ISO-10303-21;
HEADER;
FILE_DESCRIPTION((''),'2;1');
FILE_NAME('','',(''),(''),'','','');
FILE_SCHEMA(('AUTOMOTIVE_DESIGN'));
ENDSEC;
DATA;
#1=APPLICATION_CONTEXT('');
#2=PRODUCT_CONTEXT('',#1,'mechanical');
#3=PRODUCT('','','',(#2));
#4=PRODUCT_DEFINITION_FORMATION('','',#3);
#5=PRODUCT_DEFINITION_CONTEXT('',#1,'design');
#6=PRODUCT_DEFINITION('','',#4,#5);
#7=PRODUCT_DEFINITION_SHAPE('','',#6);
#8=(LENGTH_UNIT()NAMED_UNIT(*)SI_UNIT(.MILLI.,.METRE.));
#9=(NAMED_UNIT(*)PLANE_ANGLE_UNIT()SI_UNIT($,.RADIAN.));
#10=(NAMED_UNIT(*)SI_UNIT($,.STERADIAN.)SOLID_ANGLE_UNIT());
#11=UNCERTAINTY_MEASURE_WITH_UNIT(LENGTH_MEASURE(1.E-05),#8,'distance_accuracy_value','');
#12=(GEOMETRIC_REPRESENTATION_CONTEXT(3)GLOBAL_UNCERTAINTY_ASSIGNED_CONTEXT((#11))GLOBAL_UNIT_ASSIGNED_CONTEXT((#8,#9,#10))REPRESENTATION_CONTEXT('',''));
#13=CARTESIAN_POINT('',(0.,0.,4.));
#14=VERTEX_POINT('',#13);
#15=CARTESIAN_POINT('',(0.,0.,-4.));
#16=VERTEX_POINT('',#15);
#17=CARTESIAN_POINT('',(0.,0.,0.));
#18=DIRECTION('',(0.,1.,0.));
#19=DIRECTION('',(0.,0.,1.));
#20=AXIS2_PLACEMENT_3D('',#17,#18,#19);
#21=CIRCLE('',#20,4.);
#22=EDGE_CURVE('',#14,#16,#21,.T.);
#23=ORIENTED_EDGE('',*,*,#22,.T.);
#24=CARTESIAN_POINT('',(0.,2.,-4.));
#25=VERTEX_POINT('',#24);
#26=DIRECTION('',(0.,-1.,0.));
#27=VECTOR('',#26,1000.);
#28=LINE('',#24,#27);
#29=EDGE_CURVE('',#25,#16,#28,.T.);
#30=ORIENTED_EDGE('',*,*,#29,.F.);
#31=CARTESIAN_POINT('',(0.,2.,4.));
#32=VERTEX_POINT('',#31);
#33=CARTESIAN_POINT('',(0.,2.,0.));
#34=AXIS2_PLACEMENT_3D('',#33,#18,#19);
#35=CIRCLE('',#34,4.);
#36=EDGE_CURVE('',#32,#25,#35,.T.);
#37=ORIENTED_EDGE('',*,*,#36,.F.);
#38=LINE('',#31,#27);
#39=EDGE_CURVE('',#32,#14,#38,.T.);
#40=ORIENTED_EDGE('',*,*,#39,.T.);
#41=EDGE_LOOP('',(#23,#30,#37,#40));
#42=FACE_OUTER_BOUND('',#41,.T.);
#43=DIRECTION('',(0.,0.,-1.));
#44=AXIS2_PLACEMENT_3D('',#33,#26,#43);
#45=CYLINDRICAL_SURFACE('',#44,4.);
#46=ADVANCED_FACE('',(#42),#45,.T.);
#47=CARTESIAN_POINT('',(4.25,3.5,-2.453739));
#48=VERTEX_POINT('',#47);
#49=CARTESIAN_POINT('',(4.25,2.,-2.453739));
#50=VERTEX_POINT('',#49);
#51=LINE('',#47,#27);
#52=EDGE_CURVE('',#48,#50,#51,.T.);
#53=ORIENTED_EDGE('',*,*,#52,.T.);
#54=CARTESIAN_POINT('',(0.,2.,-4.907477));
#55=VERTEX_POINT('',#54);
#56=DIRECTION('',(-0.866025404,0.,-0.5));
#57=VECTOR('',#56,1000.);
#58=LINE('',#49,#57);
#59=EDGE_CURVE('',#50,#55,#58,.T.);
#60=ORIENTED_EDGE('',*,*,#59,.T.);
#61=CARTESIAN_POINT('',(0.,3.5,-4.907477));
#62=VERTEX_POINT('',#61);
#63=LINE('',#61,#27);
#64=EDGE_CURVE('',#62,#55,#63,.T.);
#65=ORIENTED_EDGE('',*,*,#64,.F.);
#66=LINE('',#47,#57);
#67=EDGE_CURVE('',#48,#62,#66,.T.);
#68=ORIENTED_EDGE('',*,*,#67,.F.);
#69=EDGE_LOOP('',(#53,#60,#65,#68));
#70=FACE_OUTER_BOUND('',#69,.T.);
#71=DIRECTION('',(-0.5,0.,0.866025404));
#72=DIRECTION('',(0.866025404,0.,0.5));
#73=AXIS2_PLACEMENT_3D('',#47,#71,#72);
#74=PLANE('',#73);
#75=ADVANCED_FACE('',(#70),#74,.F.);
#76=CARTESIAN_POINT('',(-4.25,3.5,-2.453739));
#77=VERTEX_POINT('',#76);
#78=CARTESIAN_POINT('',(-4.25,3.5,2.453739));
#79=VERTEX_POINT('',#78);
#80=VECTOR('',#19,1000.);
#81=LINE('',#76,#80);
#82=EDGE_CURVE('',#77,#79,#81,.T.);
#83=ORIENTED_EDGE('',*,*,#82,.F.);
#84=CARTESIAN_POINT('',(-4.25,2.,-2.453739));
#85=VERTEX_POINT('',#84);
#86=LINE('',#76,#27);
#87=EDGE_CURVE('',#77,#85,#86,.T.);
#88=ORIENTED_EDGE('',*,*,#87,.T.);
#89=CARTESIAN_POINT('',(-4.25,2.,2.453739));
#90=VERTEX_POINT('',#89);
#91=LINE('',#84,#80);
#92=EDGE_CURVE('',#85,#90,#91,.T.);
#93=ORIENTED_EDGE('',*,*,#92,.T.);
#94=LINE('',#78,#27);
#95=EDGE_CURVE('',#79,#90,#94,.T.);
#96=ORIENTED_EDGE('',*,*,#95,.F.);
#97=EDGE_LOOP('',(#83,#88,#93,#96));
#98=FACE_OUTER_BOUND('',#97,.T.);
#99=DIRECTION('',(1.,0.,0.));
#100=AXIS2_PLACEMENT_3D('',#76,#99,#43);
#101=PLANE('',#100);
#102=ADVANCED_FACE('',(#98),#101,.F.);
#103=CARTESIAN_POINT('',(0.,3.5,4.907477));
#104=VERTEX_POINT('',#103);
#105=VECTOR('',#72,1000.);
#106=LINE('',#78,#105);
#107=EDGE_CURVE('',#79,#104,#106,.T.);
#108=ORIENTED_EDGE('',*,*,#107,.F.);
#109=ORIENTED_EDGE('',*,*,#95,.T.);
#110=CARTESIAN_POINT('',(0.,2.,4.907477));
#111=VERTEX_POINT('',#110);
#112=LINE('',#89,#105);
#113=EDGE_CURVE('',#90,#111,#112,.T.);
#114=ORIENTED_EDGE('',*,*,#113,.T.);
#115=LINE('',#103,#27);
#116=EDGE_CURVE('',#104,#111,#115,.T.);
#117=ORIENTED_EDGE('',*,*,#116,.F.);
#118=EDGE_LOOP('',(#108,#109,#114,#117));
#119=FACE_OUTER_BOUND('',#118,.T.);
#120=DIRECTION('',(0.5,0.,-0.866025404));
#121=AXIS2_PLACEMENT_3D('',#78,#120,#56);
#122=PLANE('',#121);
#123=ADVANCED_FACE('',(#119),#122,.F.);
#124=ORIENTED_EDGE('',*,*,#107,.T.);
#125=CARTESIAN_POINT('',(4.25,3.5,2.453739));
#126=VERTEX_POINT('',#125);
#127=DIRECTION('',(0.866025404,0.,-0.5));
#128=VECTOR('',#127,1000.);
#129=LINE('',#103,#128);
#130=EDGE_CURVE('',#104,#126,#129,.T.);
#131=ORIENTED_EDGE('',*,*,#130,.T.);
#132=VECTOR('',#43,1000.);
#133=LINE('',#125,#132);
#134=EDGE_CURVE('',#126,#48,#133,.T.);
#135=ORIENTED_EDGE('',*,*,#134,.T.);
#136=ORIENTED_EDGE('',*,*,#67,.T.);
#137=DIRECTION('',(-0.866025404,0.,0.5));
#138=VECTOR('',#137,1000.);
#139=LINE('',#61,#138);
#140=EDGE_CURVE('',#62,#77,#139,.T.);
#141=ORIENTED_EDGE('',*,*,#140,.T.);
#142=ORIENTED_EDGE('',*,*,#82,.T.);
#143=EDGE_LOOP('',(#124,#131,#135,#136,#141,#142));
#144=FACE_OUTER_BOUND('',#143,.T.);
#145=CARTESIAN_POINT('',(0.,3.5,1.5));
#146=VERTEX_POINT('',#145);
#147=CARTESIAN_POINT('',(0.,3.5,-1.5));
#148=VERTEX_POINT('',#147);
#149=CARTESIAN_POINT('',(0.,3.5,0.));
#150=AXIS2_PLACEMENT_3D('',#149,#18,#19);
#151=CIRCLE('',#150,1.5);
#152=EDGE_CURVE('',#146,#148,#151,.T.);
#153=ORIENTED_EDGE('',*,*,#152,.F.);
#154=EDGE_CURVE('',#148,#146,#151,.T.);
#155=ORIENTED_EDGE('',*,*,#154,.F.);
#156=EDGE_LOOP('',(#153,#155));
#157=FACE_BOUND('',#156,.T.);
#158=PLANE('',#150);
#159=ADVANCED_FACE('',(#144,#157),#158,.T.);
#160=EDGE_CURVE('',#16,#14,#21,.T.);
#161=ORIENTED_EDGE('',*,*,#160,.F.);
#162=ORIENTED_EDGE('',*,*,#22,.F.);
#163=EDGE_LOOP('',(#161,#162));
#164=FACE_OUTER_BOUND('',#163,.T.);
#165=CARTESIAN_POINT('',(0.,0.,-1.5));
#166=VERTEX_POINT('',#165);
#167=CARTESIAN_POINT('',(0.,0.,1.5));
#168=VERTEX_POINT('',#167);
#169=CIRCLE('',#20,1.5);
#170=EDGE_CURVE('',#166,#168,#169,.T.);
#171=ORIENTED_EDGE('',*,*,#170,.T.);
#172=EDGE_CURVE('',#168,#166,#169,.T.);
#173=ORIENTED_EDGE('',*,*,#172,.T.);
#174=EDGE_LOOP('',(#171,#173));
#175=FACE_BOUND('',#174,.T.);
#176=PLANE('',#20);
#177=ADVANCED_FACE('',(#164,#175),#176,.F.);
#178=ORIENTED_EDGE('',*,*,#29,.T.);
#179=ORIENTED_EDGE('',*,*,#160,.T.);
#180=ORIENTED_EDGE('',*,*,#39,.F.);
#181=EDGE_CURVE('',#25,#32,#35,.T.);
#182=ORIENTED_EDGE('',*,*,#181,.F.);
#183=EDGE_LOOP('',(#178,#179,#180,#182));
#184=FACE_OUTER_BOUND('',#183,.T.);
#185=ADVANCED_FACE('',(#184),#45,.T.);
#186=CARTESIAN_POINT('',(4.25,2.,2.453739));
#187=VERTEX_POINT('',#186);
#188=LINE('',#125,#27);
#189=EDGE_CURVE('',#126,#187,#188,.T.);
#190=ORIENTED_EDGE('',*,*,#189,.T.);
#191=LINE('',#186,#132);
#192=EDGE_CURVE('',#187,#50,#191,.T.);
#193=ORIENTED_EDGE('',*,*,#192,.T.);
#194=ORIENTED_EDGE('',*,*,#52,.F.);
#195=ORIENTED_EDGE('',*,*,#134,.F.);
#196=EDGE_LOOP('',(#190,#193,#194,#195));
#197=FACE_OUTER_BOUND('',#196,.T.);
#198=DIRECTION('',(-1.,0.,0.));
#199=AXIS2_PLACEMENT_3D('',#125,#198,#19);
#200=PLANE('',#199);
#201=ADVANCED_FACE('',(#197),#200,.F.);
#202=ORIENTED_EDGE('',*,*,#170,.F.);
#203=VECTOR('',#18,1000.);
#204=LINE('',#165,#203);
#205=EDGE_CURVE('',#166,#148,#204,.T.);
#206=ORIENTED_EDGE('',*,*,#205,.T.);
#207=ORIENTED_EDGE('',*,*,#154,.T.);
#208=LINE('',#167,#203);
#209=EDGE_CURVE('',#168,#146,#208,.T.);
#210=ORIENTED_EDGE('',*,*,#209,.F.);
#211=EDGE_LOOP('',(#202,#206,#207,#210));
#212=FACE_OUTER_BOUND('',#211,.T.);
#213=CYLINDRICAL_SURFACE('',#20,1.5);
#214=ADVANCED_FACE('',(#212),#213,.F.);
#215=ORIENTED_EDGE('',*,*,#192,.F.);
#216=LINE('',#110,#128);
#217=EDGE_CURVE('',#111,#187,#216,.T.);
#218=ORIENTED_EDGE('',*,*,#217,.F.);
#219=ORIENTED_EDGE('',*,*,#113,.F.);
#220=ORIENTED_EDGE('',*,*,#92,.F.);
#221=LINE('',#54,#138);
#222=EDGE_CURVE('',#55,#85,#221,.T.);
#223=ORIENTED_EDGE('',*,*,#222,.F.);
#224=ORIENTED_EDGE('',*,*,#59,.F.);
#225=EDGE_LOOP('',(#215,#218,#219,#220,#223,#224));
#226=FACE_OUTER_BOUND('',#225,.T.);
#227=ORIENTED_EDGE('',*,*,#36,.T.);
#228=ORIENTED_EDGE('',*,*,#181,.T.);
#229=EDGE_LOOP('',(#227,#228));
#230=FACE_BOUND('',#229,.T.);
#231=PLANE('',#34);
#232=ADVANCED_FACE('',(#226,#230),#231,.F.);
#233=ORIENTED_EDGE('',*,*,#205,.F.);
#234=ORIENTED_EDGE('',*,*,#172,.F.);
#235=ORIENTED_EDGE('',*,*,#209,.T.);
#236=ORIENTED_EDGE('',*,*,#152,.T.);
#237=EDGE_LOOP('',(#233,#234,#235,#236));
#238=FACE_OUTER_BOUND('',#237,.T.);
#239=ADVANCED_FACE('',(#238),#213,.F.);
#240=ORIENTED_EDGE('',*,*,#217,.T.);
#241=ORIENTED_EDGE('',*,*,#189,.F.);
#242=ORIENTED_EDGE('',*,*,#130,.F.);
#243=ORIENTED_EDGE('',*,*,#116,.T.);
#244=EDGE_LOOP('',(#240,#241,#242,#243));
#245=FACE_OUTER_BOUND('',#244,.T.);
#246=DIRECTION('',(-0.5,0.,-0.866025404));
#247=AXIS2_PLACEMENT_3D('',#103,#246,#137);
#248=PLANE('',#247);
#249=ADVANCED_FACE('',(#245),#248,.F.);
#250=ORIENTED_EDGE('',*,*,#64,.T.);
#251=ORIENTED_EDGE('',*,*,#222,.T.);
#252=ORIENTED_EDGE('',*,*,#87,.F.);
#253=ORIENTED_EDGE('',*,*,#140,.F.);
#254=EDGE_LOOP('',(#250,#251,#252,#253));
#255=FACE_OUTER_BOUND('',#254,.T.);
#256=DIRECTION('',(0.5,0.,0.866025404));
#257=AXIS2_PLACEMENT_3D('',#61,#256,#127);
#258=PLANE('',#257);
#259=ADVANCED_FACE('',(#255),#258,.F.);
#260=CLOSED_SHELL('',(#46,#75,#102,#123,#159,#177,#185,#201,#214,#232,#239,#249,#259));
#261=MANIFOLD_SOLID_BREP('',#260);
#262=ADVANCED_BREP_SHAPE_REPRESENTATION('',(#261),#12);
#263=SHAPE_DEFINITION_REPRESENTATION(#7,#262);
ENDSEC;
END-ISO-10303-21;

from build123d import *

# Parameters (mm, degrees)
SKETCH1_R           = 4
BOSS_EXTRUDE1_DEPTH = 2
BOSS_EXTRUDE2_DEPTH = 1.5
SKETCH3_R           = 1.5
CUT_EXTRUDE1_DEPTH  = 8.375353099


with BuildPart() as part:
    # Sketch1 → Boss-Extrude1 (new body)
    with BuildSketch(Plane(origin=(0, 0, 0), x_dir=(1, 0, 0), z_dir=(0, 1, 0))):
        with Locations(Location((0, 0, 0), (0, 0, 270))):
            Circle(SKETCH1_R)
    extrude(amount=BOSS_EXTRUDE1_DEPTH)

    # Sketch2 → Boss-Extrude2 (add)
    with BuildSketch(Plane(origin=(0, 2, 0), x_dir=(1, 0, 0), z_dir=(0, 1, 0))):
        Polygon((0, 4.907477288), (-4.25, 2.453738644), (-4.25, -2.453738644), (0, -4.907477288), (4.25, -2.453738644), (4.25, 2.453738644), align=None)
    extrude(amount=BOSS_EXTRUDE2_DEPTH)

    # Sketch3 → Cut-Extrude1 (cut, through all)
    with BuildSketch(Plane(origin=(0, 3.5, 0), x_dir=(1, 0, 0), z_dir=(0, 1, 0))):
        with Locations(Location((0, 0, 0), (0, 0, 270))):
            Circle(SKETCH3_R)
    extrude(amount=-CUT_EXTRUDE1_DEPTH, mode=Mode.SUBTRACT)


solid = part.part
